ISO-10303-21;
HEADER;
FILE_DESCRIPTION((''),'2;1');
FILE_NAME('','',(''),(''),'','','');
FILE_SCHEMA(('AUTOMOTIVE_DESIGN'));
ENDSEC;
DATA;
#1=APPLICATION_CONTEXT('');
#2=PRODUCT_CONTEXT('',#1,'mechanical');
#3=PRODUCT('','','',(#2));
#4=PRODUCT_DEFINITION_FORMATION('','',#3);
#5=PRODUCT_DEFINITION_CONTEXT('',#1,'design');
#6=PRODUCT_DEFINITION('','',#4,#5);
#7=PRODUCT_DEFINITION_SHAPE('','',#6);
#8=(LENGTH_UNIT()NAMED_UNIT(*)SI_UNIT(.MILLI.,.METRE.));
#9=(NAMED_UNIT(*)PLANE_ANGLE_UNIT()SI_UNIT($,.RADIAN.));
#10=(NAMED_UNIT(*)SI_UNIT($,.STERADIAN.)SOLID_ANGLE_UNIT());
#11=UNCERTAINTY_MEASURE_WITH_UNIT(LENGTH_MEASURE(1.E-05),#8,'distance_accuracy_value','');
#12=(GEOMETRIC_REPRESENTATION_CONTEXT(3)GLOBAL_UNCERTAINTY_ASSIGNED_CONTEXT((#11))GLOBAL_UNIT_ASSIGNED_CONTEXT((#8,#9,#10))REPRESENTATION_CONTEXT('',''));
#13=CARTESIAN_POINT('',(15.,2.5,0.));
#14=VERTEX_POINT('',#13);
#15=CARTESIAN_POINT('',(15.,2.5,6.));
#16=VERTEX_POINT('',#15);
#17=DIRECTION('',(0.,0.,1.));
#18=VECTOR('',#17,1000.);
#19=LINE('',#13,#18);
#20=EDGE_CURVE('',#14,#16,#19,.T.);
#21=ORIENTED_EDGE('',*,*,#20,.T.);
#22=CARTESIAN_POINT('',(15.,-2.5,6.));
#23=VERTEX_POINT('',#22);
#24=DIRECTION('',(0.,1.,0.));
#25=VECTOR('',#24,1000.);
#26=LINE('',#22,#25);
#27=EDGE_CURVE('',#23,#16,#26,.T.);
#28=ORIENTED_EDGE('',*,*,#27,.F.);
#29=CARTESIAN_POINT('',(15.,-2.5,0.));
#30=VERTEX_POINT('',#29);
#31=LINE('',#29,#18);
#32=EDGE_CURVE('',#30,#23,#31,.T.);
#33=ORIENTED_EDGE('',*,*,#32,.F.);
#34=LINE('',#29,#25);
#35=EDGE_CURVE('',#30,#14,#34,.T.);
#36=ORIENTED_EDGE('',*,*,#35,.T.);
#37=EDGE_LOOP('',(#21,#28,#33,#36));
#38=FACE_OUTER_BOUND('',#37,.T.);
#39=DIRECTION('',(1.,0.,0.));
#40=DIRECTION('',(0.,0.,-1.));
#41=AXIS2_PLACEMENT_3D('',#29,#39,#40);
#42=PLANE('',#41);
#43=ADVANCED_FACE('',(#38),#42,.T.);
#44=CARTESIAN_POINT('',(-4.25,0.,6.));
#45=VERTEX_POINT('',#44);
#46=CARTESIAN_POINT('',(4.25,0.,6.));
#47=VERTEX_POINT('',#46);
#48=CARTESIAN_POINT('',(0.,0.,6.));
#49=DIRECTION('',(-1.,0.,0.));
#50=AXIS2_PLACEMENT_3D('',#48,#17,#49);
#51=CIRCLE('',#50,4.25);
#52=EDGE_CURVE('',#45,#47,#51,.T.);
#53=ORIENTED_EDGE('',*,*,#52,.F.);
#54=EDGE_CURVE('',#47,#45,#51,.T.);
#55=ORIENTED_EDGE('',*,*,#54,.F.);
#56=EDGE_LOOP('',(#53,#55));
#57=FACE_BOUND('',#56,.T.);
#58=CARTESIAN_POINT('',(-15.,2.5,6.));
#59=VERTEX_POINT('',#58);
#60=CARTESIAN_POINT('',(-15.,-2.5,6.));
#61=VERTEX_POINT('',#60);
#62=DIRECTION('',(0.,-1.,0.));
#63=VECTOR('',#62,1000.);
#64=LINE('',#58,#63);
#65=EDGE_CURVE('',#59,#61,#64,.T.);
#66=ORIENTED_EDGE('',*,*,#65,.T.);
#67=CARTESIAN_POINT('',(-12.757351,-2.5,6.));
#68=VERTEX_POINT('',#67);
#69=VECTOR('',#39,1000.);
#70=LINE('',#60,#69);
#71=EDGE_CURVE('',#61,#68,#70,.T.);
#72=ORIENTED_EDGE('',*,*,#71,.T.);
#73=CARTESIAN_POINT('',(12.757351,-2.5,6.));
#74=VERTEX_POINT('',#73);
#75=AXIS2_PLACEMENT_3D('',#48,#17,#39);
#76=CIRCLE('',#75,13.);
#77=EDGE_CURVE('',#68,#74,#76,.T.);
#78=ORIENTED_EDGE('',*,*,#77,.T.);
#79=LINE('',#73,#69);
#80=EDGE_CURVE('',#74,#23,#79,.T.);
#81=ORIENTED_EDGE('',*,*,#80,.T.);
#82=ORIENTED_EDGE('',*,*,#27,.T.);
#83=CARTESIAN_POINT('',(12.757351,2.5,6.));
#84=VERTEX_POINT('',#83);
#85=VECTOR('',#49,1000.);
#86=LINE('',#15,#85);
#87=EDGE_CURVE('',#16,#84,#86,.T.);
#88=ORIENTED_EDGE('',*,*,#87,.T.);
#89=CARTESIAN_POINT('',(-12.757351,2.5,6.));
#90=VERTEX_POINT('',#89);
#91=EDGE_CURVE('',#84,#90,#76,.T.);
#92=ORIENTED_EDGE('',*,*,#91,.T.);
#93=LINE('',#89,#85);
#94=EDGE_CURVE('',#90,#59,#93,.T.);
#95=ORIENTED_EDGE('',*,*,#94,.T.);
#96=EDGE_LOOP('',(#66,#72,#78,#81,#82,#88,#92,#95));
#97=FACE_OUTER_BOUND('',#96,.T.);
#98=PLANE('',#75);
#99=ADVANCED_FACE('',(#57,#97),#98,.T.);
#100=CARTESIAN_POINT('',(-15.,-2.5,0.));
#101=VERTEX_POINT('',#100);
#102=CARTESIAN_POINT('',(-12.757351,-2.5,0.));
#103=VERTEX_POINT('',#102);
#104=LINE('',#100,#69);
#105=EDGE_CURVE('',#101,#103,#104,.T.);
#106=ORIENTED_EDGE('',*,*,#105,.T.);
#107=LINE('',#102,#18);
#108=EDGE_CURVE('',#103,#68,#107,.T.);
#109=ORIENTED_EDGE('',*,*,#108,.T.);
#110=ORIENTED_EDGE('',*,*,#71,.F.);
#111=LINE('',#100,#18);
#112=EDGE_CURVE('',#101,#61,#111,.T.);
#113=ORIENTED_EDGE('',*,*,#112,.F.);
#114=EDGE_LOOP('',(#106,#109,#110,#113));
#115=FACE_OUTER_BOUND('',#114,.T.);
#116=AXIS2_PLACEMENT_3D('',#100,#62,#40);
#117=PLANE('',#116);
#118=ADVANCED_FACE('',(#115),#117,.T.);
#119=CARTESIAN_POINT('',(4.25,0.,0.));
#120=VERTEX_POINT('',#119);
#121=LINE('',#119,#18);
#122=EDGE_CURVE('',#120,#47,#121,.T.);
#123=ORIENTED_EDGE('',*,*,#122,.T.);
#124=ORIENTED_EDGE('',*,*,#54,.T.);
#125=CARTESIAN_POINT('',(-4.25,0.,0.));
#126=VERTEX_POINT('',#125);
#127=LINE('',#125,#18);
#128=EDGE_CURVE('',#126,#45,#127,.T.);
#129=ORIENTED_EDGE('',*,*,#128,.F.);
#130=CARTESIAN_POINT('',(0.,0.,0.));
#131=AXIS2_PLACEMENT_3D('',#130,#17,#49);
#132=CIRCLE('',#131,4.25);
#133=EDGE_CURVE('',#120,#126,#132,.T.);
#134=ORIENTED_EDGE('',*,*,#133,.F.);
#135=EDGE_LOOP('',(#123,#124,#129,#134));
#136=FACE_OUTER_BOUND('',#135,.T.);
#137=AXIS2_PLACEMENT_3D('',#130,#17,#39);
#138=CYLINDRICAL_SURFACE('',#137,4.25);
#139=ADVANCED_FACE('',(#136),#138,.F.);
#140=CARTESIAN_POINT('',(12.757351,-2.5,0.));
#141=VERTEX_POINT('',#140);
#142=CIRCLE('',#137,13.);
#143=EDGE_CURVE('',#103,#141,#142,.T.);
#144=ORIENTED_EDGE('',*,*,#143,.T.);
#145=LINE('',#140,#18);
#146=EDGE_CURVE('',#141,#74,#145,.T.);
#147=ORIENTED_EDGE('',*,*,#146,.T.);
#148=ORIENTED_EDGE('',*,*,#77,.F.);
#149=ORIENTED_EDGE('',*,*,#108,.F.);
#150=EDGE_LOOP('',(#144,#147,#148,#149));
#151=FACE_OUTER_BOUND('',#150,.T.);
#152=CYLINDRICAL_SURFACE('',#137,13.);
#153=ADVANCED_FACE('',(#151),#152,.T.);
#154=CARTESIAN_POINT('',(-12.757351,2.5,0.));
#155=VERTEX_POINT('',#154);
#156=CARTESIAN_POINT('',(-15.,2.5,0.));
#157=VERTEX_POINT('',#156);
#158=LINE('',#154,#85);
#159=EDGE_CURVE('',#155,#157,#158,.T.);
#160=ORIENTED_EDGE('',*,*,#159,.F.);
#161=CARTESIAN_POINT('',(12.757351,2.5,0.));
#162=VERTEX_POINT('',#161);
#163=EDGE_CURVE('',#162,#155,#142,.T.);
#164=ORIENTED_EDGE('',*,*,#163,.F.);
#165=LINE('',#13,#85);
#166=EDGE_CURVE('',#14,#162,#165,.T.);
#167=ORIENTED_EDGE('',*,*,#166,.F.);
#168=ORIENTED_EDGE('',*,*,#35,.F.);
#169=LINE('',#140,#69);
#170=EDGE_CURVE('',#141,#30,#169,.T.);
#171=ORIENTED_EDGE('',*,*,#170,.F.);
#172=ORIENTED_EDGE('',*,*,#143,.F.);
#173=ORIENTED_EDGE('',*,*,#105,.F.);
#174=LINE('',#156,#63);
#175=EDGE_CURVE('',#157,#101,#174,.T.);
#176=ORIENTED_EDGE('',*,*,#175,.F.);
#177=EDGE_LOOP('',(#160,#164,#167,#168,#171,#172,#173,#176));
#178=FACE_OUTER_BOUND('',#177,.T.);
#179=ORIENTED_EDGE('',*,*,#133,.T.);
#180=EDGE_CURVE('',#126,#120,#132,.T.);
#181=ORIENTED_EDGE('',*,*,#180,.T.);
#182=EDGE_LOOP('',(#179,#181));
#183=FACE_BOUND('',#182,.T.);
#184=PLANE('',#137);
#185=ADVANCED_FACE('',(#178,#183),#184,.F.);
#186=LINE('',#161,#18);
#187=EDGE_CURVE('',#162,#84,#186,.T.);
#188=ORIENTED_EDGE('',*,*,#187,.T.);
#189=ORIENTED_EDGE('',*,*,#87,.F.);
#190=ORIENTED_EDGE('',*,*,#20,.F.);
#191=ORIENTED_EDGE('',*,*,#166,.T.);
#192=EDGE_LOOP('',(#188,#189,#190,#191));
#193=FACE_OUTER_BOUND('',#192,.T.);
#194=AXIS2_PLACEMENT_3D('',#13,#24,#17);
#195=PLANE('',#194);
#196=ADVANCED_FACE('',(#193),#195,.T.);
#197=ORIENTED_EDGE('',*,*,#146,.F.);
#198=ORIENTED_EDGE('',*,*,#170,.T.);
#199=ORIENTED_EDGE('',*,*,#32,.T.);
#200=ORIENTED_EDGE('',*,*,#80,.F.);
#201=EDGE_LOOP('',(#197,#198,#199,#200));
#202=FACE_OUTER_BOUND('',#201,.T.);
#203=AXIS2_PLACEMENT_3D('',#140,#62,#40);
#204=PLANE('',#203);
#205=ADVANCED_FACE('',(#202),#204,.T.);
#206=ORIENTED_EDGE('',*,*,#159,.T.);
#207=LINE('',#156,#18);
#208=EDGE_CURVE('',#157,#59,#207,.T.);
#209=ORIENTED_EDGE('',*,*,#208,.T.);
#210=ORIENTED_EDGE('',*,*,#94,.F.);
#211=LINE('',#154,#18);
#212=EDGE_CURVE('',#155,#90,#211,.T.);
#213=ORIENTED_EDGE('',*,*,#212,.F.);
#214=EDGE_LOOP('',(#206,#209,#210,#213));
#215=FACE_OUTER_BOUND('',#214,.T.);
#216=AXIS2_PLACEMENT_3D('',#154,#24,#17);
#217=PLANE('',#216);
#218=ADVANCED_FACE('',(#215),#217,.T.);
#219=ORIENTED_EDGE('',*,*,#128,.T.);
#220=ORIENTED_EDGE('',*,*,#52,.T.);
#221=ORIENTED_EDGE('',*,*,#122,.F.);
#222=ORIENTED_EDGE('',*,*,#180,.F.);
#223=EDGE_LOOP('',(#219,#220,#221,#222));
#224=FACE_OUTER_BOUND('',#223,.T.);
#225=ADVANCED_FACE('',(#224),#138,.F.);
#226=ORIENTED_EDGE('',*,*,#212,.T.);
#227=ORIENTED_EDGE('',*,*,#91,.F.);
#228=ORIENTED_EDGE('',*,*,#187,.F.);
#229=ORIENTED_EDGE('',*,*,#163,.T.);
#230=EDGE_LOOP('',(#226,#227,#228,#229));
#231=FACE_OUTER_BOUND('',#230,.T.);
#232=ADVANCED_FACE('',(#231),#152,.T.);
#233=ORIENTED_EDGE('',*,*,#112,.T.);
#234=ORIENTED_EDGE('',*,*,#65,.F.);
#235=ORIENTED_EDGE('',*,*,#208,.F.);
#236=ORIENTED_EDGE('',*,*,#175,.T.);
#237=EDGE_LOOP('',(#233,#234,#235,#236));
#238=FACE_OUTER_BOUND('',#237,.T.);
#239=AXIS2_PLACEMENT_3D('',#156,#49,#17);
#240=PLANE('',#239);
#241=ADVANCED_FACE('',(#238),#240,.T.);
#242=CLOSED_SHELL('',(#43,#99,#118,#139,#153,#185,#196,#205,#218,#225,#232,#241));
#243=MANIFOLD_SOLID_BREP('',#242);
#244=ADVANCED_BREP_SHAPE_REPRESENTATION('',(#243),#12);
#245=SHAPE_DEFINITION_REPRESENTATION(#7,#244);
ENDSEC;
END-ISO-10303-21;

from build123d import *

# Parameters (mm, degrees)
SKETCH1_R           = 4.25
BOSS_EXTRUDE1_DEPTH = 6


with BuildPart() as part:
    # Sketch1 → Boss-Extrude1 (new body)
    with BuildSketch(Plane.XY.offset(6)):
        with BuildLine():
            Line((-12.757350822, 2.5), (-15, 2.5))
            Line((-15, 2.5), (-15, -2.5))
            Line((-15, -2.5), (-12.757350822, -2.5))
            ThreePointArc((-12.757350822, -2.5), (0, -13), (12.757350822, -2.5))
            Line((12.757350822, -2.5), (15, -2.5))
            Line((15, -2.5), (15, 2.5))
            Line((15, 2.5), (12.757350822, 2.5))
            ThreePointArc((12.757350822, 2.5), (0, 13), (-12.757350822, 2.5))
        make_face()
        with Locations(Location((0, 0, 0), (0, 0, 180))):
            Circle(SKETCH1_R, mode=Mode.SUBTRACT)
    extrude(amount=-BOSS_EXTRUDE1_DEPTH)


solid = part.part
